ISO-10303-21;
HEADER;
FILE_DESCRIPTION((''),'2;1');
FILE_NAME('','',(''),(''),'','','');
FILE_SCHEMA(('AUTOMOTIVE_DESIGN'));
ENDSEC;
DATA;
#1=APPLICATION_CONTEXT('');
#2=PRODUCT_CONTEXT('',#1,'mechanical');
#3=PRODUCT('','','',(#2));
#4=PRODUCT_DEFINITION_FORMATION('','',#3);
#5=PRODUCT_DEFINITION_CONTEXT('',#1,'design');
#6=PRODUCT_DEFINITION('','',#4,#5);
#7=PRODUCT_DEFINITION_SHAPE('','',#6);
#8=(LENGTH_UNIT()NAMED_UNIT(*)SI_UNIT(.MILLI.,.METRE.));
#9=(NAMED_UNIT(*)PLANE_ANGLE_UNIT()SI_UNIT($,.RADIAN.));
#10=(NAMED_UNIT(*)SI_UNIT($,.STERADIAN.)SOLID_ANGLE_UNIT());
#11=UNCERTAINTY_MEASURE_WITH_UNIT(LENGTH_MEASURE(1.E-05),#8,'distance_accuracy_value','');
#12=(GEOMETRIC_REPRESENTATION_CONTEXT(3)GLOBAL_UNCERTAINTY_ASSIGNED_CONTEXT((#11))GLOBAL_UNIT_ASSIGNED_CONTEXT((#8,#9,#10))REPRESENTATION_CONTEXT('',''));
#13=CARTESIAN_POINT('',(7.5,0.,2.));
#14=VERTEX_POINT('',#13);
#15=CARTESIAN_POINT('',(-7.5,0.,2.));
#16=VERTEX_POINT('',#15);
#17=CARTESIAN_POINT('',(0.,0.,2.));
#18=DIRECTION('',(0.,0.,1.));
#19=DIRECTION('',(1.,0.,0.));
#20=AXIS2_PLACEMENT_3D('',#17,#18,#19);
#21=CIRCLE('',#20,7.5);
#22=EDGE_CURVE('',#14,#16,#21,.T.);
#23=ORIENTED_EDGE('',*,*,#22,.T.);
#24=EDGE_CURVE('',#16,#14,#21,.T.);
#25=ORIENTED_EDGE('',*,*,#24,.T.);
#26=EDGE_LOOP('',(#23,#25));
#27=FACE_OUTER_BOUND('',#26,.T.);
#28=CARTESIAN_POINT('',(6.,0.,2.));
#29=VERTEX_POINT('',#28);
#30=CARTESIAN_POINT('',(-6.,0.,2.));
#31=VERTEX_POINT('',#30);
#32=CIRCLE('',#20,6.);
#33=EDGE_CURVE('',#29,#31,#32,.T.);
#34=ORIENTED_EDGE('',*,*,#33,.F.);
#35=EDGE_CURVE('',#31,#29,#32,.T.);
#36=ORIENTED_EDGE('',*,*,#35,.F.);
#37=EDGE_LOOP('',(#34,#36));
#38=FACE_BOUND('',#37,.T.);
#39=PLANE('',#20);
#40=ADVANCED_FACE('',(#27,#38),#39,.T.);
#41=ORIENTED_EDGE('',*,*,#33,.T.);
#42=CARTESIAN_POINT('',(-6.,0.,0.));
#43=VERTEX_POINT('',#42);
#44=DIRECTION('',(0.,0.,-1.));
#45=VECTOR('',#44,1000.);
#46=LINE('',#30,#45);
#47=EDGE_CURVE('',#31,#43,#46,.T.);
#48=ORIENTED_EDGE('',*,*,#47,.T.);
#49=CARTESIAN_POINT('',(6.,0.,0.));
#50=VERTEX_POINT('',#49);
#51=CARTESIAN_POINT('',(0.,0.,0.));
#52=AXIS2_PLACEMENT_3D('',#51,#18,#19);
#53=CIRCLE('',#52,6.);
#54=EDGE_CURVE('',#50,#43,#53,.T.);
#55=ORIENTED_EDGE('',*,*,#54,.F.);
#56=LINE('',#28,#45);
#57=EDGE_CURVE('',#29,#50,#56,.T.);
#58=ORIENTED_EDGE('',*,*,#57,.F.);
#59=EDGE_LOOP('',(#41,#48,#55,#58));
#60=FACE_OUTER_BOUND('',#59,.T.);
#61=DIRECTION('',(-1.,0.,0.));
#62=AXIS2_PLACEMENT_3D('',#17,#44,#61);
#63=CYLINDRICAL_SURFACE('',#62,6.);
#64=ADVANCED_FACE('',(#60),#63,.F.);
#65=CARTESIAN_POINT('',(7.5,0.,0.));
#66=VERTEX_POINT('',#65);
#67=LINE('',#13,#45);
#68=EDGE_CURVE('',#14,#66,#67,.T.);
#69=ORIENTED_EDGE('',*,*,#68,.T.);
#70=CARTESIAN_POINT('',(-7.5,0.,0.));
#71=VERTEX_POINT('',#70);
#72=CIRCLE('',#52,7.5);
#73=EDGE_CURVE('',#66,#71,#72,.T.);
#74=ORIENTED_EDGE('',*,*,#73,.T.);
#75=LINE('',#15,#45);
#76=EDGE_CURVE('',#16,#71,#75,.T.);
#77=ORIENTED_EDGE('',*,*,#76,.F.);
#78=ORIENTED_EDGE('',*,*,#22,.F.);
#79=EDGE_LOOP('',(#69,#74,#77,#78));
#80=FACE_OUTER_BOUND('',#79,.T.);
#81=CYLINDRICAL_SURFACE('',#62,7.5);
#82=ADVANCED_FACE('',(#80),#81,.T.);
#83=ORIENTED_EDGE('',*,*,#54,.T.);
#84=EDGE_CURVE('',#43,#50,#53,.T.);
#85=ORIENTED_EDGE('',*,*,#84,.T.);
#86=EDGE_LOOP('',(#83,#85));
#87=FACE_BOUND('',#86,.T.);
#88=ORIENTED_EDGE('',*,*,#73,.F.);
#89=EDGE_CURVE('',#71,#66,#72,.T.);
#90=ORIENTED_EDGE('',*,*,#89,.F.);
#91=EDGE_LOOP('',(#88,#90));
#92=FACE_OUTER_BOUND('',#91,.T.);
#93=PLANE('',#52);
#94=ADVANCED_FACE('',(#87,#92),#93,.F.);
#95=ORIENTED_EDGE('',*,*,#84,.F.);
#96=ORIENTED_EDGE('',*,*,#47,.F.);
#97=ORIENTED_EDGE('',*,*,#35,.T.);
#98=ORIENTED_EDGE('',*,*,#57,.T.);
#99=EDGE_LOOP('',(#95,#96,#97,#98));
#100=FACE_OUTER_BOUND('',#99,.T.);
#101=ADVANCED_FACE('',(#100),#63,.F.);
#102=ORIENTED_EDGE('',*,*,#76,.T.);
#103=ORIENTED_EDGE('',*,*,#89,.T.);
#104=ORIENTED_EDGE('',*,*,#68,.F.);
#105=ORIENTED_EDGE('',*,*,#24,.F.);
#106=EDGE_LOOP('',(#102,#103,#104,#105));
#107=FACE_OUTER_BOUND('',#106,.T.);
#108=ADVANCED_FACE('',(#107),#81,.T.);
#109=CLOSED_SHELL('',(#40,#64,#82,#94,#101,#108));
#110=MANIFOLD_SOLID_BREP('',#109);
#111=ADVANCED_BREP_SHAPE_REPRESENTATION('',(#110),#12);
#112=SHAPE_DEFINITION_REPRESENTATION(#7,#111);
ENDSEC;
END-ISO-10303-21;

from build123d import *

# Parameters (mm, degrees)
SKETCH2_R           = 7.5
SKETCH2_R_2         = 6
BOSS_EXTRUDE1_DEPTH = 2


with BuildPart() as part:
    # Sketch2 → Boss-Extrude1 (new body)
    with BuildSketch(Plane.XY):
        Circle(SKETCH2_R)
        Circle(SKETCH2_R_2, mode=Mode.SUBTRACT)
    extrude(amount=BOSS_EXTRUDE1_DEPTH)


solid = part.part
